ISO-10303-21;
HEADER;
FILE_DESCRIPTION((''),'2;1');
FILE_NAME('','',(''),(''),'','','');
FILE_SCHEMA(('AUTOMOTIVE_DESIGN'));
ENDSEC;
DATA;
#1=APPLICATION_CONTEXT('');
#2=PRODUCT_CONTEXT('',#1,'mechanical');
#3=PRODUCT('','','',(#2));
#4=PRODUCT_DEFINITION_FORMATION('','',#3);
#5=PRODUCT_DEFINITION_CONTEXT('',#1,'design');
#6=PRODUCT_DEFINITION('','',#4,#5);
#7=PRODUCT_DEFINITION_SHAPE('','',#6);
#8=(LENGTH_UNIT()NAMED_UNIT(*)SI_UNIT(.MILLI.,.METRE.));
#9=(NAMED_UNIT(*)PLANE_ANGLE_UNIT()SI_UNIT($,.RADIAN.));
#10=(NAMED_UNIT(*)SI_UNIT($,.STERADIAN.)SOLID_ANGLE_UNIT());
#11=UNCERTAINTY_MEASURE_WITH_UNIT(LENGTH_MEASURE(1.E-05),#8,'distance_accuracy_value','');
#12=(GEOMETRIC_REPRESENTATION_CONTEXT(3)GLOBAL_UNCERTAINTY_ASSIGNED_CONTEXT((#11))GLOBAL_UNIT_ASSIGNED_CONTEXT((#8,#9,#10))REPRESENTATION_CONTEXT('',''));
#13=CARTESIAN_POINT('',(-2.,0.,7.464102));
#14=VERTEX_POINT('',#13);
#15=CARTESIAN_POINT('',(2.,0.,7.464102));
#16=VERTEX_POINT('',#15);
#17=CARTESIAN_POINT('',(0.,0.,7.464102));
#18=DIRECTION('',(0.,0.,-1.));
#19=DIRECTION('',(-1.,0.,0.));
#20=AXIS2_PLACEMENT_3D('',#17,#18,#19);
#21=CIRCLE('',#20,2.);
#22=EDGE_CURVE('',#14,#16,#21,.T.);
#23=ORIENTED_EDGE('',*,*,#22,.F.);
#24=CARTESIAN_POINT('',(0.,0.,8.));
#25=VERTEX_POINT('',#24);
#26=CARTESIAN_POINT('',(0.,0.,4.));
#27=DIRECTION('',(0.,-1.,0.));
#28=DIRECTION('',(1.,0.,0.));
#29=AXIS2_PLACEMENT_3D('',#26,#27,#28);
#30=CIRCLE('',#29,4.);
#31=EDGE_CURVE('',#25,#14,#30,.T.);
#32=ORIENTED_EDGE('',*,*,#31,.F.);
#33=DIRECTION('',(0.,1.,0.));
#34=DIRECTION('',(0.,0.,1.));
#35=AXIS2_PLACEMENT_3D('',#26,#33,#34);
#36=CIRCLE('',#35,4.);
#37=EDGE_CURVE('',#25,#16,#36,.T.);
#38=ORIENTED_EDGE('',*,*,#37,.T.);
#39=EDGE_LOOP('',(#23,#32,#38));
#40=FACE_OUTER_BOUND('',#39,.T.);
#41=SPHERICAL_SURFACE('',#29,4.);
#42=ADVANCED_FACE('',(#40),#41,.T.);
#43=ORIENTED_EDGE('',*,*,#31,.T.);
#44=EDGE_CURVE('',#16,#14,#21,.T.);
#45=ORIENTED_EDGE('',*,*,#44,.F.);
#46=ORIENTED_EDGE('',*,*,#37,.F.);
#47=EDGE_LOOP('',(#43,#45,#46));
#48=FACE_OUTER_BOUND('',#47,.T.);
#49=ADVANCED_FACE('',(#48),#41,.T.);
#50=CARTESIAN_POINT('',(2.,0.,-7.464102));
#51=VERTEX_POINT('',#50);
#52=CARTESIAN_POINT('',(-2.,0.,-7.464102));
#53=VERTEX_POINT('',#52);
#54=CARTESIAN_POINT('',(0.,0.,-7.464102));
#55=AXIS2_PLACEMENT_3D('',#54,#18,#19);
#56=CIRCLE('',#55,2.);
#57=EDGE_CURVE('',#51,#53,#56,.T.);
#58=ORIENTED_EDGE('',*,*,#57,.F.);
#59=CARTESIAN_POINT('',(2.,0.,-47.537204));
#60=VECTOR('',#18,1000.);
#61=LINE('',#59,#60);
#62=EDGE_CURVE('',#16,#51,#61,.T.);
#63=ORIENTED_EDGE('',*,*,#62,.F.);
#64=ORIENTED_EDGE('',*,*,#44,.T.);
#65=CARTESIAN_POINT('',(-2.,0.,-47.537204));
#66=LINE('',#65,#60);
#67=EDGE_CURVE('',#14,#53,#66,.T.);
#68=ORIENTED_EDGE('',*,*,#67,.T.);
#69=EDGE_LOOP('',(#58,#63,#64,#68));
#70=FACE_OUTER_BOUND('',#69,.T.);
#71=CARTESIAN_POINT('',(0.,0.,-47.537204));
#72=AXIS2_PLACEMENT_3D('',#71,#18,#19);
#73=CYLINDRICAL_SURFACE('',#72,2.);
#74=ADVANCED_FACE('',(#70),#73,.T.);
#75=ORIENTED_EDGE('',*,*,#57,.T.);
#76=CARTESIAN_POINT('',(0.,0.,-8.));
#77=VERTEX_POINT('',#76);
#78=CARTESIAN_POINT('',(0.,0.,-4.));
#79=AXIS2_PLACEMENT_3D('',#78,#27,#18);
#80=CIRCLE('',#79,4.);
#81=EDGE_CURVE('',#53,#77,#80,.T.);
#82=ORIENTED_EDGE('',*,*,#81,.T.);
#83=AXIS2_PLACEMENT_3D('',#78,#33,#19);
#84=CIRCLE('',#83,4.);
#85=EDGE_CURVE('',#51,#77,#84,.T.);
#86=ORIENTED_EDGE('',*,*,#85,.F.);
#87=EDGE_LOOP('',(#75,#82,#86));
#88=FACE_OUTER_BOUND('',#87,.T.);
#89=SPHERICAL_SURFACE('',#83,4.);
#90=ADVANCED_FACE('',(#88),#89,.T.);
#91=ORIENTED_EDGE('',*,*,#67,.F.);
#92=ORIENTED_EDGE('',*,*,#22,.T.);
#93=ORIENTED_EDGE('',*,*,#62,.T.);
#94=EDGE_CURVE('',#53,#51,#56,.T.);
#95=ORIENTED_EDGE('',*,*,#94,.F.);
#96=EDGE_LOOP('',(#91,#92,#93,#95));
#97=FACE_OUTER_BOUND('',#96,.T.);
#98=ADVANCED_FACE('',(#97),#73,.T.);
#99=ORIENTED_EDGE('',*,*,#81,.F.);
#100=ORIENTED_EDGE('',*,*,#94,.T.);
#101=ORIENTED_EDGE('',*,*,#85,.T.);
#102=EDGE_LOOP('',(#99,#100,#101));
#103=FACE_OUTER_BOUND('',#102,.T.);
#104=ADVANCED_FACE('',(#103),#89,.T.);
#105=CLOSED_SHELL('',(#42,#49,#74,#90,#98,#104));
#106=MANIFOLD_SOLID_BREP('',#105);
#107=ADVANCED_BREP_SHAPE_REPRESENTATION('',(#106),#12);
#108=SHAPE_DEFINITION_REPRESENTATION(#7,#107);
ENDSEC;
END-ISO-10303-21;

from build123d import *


with BuildPart() as part:
    # Logo3_bib1 → Revolve1 (revolve)
    with BuildSketch(Plane(origin=(0, 0, 0), x_dir=(-1, 0, 0), z_dir=(0, -1, 0))):
        with BuildLine():
            Line((0, 8), (0, -8))
            ThreePointArc((0, -8), (1.03527618, -7.863703305), (2, -7.464101615))
            Line((2, -7.464101615), (2, 7.464101615))
            ThreePointArc((2, 7.464101615), (1.03527618, 7.863703305), (0, 8))
        make_face()
    revolve(axis=Axis((0, 0, -47.537203702), (0, 0, 1)))


solid = part.part
